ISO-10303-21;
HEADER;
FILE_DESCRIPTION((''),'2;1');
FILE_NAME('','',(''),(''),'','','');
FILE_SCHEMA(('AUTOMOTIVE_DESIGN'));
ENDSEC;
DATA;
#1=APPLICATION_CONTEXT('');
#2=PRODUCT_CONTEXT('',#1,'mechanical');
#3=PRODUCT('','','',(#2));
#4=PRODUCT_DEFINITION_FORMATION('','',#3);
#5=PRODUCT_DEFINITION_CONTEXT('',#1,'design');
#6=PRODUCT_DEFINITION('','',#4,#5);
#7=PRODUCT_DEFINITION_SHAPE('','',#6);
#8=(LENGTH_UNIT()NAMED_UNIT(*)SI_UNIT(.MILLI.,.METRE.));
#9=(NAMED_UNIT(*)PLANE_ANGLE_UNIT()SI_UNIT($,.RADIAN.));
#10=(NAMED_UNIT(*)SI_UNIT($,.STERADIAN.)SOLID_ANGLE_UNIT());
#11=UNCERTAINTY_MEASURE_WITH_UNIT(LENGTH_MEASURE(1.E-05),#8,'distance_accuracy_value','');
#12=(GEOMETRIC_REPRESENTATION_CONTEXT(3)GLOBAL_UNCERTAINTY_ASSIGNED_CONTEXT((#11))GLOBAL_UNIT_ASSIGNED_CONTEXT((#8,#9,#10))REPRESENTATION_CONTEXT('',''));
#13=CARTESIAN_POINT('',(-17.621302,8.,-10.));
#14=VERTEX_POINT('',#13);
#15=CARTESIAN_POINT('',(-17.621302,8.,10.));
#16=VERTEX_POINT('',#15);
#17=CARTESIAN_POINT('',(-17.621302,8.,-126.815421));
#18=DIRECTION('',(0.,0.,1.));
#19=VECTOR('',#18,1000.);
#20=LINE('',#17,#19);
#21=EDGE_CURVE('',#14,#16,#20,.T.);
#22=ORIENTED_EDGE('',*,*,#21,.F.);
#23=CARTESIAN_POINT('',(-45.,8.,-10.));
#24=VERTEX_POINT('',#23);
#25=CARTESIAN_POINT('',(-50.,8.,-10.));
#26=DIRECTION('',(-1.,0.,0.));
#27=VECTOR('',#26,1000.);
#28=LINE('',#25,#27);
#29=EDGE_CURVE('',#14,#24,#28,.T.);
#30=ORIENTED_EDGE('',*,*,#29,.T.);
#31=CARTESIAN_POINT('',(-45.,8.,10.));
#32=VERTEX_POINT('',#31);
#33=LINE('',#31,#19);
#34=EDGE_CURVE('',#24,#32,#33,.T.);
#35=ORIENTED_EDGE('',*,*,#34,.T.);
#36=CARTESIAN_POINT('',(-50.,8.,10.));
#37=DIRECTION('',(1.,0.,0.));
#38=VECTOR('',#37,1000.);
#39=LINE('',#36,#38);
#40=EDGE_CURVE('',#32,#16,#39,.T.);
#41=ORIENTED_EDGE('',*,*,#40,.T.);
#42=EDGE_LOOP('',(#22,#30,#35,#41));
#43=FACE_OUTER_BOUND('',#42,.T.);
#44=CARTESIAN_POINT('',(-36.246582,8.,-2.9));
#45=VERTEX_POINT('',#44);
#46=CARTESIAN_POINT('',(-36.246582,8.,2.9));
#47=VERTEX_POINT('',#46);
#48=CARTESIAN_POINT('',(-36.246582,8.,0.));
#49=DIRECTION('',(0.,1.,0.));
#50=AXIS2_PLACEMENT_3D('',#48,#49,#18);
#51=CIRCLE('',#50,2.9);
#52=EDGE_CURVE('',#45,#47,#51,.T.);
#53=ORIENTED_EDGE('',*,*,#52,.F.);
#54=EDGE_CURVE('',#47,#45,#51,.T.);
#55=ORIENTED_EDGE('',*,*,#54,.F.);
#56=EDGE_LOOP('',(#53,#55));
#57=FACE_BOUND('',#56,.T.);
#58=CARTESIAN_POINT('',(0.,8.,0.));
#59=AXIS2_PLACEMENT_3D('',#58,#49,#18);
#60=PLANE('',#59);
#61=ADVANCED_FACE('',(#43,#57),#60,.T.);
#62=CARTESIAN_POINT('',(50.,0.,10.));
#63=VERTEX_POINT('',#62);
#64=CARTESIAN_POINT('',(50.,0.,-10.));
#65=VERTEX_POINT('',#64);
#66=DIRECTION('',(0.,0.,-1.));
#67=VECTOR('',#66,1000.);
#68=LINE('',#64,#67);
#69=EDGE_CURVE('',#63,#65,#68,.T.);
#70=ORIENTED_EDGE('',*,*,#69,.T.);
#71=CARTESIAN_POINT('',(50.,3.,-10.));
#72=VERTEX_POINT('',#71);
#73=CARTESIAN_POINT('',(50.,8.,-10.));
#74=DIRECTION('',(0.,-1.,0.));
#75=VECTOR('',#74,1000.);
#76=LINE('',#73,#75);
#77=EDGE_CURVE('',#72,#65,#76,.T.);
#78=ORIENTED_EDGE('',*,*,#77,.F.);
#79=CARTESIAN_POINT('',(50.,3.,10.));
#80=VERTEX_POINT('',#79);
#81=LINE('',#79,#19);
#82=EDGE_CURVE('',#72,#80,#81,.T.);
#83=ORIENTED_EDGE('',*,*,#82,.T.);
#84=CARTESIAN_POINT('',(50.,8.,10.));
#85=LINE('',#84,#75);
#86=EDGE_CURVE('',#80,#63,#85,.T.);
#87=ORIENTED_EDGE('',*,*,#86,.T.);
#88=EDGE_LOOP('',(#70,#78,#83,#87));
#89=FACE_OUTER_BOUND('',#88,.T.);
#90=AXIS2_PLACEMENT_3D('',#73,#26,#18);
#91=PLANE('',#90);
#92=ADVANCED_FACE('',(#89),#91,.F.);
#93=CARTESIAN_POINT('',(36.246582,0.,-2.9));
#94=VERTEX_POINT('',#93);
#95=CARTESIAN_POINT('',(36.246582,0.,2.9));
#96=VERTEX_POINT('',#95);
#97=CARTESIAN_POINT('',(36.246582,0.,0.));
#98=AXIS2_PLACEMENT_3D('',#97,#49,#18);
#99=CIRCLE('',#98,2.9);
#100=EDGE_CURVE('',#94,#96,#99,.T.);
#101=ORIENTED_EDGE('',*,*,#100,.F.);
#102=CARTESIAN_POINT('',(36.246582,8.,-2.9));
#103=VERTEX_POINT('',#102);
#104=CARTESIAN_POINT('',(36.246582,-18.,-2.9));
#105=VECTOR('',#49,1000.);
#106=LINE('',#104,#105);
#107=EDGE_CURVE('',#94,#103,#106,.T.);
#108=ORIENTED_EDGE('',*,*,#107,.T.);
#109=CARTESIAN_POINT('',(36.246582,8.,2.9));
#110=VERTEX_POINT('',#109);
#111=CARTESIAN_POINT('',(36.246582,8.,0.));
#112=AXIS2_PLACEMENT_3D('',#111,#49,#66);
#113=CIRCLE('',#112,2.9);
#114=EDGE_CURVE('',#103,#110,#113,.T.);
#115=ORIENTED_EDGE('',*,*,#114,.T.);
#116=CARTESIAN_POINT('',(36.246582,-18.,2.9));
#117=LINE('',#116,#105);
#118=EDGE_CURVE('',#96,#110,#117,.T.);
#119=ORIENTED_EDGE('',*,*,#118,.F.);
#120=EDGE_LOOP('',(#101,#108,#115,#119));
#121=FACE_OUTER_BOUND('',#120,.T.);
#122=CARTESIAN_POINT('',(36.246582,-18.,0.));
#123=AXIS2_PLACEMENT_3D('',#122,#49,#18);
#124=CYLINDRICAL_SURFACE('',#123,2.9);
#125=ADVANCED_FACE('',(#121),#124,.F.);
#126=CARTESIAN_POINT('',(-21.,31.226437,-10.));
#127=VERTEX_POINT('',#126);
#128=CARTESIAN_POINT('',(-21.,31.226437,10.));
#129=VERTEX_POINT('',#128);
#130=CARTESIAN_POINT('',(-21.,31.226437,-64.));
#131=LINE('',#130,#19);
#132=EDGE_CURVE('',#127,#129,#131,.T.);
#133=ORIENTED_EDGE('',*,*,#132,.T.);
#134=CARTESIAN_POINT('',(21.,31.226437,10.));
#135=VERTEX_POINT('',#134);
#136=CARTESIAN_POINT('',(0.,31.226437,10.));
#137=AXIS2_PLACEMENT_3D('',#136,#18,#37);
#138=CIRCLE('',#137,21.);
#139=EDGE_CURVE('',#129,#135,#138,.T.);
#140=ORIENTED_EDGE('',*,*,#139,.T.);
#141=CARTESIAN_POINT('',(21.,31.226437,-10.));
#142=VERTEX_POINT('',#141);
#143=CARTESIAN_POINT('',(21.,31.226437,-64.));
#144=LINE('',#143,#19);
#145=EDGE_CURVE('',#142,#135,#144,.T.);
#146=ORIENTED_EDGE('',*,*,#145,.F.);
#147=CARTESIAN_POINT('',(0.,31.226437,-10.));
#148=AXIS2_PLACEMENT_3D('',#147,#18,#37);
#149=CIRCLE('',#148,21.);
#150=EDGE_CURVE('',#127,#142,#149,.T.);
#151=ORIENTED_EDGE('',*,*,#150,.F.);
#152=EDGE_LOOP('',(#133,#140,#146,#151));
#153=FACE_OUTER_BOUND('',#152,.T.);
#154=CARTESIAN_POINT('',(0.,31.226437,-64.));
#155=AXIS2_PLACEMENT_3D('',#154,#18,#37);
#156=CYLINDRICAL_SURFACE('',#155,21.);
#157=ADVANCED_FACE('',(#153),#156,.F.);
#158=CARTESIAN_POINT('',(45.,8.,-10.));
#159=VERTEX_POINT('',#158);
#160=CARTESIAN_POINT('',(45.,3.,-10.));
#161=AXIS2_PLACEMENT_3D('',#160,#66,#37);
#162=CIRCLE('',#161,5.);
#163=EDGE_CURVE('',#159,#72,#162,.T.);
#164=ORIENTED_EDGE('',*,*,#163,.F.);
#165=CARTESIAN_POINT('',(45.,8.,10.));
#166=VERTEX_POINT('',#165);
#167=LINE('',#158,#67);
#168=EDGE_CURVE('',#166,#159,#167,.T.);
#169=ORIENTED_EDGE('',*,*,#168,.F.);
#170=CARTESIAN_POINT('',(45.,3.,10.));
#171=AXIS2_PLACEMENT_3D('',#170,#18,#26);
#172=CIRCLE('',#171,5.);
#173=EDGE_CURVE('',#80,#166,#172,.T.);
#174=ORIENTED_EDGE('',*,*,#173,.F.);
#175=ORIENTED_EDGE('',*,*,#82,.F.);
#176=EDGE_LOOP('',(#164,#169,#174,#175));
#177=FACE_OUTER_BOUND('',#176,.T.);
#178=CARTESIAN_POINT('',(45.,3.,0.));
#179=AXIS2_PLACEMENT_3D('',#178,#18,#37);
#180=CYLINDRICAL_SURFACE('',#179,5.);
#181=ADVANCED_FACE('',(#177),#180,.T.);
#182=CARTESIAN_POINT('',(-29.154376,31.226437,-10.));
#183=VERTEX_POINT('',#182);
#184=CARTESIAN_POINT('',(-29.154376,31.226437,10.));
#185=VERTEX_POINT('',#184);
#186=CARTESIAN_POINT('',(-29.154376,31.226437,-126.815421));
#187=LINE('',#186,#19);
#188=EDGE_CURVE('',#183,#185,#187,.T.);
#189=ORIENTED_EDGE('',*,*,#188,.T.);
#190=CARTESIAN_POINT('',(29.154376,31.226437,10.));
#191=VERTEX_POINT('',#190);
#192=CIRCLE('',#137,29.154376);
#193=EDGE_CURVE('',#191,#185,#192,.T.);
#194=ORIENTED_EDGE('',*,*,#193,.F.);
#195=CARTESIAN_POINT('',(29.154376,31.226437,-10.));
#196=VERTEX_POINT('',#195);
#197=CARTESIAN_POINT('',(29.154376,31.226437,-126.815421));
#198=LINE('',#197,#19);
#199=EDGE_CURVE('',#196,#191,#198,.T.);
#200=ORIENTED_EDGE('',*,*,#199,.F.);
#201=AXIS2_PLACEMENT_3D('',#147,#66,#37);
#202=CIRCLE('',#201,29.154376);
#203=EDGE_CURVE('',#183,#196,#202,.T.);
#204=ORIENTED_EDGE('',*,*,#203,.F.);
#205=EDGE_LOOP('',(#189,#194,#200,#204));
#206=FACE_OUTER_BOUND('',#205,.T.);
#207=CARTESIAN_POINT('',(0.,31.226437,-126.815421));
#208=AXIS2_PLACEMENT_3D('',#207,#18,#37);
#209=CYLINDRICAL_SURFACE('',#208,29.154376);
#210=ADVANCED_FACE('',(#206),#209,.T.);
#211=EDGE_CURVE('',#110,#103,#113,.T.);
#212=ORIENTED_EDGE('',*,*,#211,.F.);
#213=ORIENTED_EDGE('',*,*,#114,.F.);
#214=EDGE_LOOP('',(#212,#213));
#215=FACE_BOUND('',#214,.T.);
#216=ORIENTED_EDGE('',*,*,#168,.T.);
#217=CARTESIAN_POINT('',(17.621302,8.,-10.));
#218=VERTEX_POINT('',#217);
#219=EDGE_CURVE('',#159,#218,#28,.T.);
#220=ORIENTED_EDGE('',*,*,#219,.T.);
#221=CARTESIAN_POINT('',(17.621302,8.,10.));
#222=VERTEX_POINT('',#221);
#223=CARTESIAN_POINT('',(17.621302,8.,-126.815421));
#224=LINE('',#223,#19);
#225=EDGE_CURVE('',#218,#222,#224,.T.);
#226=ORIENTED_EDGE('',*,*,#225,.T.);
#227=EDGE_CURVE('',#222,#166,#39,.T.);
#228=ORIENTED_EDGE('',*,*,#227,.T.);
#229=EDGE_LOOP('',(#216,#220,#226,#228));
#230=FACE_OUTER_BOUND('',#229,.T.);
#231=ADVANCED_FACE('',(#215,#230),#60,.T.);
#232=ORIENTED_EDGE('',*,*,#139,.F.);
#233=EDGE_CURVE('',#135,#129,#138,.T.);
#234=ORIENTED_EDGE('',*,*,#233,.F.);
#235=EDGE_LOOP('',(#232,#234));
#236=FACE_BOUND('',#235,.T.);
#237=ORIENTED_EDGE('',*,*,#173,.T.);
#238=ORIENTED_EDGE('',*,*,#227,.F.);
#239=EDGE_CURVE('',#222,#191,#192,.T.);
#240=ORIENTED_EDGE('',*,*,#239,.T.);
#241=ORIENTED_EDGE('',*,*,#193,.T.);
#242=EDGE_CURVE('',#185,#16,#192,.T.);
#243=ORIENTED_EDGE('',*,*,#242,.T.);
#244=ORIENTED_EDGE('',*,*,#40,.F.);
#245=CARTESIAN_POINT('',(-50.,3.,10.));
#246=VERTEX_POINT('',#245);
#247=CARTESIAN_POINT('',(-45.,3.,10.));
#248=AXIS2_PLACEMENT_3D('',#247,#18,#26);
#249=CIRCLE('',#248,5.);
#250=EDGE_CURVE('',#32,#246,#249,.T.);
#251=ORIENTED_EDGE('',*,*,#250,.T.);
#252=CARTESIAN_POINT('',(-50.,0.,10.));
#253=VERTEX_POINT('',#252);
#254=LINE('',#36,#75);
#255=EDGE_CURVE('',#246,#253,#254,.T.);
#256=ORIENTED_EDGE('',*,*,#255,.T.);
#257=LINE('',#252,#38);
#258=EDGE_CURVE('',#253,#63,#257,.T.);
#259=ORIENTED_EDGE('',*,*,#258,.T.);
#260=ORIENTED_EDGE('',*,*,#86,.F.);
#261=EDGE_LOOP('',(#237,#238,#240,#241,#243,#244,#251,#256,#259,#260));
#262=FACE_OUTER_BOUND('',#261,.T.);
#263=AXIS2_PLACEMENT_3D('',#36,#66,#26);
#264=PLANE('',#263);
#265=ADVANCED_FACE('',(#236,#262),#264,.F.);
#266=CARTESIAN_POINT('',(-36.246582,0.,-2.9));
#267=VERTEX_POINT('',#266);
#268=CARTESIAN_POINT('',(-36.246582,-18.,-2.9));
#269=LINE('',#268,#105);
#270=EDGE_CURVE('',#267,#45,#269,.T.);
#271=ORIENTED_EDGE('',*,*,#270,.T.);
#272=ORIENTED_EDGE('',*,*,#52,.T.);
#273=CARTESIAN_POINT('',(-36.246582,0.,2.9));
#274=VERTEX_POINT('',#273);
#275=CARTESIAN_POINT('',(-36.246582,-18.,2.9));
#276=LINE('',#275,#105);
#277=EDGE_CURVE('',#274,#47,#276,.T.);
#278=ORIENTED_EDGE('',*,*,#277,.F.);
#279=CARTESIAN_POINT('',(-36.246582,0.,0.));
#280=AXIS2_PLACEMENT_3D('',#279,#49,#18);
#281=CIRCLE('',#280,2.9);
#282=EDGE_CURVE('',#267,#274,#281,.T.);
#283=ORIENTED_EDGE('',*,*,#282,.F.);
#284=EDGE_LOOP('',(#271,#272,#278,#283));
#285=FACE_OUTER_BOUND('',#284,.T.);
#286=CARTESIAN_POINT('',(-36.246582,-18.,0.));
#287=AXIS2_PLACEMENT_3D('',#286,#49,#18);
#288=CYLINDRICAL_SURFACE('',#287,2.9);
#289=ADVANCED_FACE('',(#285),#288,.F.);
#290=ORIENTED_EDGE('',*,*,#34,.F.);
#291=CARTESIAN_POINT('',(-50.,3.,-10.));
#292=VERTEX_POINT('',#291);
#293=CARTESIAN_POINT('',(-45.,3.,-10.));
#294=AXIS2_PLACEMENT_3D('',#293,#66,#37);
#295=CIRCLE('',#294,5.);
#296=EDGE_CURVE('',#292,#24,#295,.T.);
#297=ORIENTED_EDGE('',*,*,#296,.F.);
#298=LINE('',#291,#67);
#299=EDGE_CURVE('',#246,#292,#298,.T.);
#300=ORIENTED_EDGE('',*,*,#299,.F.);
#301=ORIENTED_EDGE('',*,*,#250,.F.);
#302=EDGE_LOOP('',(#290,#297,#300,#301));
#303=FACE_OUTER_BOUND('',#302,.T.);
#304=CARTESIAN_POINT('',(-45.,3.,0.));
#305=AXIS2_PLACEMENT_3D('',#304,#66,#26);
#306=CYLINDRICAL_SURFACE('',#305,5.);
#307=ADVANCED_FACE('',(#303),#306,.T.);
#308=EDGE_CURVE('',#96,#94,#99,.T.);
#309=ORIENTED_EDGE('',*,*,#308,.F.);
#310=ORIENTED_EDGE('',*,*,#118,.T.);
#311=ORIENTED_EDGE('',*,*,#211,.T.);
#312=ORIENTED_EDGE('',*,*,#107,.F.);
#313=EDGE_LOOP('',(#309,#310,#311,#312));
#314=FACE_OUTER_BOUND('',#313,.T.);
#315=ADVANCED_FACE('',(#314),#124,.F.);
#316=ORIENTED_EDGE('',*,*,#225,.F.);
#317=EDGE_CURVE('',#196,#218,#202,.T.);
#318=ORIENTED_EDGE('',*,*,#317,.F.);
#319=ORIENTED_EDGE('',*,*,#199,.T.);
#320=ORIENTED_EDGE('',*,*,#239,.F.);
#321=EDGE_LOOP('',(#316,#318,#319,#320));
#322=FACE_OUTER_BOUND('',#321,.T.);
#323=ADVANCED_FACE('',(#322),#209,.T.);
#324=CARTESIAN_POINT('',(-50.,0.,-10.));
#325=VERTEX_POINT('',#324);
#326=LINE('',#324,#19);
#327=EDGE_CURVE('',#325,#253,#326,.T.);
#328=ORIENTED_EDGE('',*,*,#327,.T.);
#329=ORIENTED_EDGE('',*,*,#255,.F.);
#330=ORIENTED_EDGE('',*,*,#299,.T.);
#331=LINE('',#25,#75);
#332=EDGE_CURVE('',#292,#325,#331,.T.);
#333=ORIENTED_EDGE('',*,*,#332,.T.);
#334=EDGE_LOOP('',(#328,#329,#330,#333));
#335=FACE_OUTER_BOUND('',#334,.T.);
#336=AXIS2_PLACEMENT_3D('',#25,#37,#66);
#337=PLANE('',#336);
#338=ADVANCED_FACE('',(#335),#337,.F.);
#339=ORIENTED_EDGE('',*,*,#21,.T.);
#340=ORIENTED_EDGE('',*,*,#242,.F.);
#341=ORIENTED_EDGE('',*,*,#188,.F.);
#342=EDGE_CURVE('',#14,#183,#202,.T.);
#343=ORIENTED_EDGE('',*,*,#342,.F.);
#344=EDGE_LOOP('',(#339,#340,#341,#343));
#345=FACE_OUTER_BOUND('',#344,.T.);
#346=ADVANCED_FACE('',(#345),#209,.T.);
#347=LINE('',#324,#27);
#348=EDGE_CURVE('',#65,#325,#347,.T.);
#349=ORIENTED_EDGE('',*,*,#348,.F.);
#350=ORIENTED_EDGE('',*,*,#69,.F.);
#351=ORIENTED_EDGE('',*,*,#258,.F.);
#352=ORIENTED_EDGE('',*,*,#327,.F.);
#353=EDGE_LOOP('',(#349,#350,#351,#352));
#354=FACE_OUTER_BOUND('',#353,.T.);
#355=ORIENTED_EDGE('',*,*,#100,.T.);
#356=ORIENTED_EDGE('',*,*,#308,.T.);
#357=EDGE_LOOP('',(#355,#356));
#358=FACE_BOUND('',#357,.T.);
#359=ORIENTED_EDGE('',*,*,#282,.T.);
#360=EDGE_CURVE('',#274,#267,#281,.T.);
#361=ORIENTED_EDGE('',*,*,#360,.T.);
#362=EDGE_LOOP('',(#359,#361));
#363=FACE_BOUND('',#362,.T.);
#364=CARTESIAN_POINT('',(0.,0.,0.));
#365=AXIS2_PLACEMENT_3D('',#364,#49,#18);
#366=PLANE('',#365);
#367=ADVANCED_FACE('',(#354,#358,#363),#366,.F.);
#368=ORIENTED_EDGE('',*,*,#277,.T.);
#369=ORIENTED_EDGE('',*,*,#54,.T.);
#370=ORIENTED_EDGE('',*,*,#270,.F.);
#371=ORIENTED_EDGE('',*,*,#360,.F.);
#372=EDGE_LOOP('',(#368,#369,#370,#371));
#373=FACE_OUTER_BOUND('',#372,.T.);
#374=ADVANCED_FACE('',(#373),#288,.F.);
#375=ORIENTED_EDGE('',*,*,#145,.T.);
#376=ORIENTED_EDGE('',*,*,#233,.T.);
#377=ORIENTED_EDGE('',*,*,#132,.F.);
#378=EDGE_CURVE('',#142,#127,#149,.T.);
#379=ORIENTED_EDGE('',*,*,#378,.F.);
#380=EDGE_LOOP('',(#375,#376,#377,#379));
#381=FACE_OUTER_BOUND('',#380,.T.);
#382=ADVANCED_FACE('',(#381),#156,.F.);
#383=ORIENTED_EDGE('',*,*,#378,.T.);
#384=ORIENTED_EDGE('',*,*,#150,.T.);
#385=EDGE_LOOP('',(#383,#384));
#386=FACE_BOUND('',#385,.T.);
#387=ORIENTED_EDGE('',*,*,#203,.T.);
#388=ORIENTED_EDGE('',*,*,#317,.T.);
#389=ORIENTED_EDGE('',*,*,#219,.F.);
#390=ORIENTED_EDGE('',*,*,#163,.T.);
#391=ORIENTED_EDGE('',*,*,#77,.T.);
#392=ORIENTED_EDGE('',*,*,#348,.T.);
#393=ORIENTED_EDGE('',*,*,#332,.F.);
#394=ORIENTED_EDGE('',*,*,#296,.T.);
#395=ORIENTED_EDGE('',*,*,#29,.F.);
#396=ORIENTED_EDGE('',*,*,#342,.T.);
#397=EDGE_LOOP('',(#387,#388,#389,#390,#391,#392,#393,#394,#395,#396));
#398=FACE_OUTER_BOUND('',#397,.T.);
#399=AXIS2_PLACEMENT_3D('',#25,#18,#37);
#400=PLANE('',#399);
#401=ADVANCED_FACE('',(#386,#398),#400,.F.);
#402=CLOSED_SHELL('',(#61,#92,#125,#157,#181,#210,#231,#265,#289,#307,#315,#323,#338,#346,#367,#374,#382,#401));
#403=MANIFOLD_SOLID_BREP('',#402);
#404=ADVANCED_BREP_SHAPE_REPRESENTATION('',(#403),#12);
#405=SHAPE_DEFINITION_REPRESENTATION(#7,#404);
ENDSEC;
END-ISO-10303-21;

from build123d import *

# Parameters (mm, degrees)
SKETCH1_W           = 100
SKETCH1_H           = 20
BOSS_EXTRUDE1_DEPTH = 8
FILLET1_R           = 5
SKETCH2_R           = 29.154376269
BOSS_EXTRUDE3_DEPTH = 20
SKETCH3_R           = 2.9
CUT_EXTRUDE1_DEPTH  = 26
SKETCH4_R           = 21
CUT_EXTRUDE2_DEPTH  = 74


with BuildPart() as part:
    # Sketch1 → Boss-Extrude1 (new body)
    with BuildSketch(Plane(origin=(0, 0, 0), x_dir=(1, 0, 0), z_dir=(0, 1, 0))):
        Rectangle(SKETCH1_W, SKETCH1_H)
    extrude(amount=BOSS_EXTRUDE1_DEPTH)

    # Fillet1
    fillet1_edges = [part.edges().sort_by_distance(p)[0] for p in [
        (-50, 8, 0),
        (50, 8, 0),
    ]]
    fillet(fillet1_edges, radius=FILLET1_R)

    # Sketch2 → Boss-Extrude3 (add)
    with BuildSketch(Plane.XY.offset(10)):
        with Locations((0, 31.226436769)):
            Circle(SKETCH2_R)
    extrude(amount=-BOSS_EXTRUDE3_DEPTH)

    # Sketch3 → Cut-Extrude1 (cut)
    with BuildSketch(Plane(origin=(0, 8, 0), x_dir=(1, 0, 0), z_dir=(0, 1, 0))):
        with Locations(Location((-36.246581996, 0, 0), (0, 0, 270))):
            Circle(SKETCH3_R)
        with Locations(Location((36.246581996, 0, 0), (0, 0, 270))):
            Circle(SKETCH3_R)
    extrude(amount=-CUT_EXTRUDE1_DEPTH, mode=Mode.SUBTRACT)

    # Sketch4 → Cut-Extrude2 (cut)
    with BuildSketch(Plane.XY.offset(10)):
        with Locations((0, 31.226436769)):
            Circle(SKETCH4_R)
    extrude(amount=-CUT_EXTRUDE2_DEPTH, mode=Mode.SUBTRACT)


solid = part.part
